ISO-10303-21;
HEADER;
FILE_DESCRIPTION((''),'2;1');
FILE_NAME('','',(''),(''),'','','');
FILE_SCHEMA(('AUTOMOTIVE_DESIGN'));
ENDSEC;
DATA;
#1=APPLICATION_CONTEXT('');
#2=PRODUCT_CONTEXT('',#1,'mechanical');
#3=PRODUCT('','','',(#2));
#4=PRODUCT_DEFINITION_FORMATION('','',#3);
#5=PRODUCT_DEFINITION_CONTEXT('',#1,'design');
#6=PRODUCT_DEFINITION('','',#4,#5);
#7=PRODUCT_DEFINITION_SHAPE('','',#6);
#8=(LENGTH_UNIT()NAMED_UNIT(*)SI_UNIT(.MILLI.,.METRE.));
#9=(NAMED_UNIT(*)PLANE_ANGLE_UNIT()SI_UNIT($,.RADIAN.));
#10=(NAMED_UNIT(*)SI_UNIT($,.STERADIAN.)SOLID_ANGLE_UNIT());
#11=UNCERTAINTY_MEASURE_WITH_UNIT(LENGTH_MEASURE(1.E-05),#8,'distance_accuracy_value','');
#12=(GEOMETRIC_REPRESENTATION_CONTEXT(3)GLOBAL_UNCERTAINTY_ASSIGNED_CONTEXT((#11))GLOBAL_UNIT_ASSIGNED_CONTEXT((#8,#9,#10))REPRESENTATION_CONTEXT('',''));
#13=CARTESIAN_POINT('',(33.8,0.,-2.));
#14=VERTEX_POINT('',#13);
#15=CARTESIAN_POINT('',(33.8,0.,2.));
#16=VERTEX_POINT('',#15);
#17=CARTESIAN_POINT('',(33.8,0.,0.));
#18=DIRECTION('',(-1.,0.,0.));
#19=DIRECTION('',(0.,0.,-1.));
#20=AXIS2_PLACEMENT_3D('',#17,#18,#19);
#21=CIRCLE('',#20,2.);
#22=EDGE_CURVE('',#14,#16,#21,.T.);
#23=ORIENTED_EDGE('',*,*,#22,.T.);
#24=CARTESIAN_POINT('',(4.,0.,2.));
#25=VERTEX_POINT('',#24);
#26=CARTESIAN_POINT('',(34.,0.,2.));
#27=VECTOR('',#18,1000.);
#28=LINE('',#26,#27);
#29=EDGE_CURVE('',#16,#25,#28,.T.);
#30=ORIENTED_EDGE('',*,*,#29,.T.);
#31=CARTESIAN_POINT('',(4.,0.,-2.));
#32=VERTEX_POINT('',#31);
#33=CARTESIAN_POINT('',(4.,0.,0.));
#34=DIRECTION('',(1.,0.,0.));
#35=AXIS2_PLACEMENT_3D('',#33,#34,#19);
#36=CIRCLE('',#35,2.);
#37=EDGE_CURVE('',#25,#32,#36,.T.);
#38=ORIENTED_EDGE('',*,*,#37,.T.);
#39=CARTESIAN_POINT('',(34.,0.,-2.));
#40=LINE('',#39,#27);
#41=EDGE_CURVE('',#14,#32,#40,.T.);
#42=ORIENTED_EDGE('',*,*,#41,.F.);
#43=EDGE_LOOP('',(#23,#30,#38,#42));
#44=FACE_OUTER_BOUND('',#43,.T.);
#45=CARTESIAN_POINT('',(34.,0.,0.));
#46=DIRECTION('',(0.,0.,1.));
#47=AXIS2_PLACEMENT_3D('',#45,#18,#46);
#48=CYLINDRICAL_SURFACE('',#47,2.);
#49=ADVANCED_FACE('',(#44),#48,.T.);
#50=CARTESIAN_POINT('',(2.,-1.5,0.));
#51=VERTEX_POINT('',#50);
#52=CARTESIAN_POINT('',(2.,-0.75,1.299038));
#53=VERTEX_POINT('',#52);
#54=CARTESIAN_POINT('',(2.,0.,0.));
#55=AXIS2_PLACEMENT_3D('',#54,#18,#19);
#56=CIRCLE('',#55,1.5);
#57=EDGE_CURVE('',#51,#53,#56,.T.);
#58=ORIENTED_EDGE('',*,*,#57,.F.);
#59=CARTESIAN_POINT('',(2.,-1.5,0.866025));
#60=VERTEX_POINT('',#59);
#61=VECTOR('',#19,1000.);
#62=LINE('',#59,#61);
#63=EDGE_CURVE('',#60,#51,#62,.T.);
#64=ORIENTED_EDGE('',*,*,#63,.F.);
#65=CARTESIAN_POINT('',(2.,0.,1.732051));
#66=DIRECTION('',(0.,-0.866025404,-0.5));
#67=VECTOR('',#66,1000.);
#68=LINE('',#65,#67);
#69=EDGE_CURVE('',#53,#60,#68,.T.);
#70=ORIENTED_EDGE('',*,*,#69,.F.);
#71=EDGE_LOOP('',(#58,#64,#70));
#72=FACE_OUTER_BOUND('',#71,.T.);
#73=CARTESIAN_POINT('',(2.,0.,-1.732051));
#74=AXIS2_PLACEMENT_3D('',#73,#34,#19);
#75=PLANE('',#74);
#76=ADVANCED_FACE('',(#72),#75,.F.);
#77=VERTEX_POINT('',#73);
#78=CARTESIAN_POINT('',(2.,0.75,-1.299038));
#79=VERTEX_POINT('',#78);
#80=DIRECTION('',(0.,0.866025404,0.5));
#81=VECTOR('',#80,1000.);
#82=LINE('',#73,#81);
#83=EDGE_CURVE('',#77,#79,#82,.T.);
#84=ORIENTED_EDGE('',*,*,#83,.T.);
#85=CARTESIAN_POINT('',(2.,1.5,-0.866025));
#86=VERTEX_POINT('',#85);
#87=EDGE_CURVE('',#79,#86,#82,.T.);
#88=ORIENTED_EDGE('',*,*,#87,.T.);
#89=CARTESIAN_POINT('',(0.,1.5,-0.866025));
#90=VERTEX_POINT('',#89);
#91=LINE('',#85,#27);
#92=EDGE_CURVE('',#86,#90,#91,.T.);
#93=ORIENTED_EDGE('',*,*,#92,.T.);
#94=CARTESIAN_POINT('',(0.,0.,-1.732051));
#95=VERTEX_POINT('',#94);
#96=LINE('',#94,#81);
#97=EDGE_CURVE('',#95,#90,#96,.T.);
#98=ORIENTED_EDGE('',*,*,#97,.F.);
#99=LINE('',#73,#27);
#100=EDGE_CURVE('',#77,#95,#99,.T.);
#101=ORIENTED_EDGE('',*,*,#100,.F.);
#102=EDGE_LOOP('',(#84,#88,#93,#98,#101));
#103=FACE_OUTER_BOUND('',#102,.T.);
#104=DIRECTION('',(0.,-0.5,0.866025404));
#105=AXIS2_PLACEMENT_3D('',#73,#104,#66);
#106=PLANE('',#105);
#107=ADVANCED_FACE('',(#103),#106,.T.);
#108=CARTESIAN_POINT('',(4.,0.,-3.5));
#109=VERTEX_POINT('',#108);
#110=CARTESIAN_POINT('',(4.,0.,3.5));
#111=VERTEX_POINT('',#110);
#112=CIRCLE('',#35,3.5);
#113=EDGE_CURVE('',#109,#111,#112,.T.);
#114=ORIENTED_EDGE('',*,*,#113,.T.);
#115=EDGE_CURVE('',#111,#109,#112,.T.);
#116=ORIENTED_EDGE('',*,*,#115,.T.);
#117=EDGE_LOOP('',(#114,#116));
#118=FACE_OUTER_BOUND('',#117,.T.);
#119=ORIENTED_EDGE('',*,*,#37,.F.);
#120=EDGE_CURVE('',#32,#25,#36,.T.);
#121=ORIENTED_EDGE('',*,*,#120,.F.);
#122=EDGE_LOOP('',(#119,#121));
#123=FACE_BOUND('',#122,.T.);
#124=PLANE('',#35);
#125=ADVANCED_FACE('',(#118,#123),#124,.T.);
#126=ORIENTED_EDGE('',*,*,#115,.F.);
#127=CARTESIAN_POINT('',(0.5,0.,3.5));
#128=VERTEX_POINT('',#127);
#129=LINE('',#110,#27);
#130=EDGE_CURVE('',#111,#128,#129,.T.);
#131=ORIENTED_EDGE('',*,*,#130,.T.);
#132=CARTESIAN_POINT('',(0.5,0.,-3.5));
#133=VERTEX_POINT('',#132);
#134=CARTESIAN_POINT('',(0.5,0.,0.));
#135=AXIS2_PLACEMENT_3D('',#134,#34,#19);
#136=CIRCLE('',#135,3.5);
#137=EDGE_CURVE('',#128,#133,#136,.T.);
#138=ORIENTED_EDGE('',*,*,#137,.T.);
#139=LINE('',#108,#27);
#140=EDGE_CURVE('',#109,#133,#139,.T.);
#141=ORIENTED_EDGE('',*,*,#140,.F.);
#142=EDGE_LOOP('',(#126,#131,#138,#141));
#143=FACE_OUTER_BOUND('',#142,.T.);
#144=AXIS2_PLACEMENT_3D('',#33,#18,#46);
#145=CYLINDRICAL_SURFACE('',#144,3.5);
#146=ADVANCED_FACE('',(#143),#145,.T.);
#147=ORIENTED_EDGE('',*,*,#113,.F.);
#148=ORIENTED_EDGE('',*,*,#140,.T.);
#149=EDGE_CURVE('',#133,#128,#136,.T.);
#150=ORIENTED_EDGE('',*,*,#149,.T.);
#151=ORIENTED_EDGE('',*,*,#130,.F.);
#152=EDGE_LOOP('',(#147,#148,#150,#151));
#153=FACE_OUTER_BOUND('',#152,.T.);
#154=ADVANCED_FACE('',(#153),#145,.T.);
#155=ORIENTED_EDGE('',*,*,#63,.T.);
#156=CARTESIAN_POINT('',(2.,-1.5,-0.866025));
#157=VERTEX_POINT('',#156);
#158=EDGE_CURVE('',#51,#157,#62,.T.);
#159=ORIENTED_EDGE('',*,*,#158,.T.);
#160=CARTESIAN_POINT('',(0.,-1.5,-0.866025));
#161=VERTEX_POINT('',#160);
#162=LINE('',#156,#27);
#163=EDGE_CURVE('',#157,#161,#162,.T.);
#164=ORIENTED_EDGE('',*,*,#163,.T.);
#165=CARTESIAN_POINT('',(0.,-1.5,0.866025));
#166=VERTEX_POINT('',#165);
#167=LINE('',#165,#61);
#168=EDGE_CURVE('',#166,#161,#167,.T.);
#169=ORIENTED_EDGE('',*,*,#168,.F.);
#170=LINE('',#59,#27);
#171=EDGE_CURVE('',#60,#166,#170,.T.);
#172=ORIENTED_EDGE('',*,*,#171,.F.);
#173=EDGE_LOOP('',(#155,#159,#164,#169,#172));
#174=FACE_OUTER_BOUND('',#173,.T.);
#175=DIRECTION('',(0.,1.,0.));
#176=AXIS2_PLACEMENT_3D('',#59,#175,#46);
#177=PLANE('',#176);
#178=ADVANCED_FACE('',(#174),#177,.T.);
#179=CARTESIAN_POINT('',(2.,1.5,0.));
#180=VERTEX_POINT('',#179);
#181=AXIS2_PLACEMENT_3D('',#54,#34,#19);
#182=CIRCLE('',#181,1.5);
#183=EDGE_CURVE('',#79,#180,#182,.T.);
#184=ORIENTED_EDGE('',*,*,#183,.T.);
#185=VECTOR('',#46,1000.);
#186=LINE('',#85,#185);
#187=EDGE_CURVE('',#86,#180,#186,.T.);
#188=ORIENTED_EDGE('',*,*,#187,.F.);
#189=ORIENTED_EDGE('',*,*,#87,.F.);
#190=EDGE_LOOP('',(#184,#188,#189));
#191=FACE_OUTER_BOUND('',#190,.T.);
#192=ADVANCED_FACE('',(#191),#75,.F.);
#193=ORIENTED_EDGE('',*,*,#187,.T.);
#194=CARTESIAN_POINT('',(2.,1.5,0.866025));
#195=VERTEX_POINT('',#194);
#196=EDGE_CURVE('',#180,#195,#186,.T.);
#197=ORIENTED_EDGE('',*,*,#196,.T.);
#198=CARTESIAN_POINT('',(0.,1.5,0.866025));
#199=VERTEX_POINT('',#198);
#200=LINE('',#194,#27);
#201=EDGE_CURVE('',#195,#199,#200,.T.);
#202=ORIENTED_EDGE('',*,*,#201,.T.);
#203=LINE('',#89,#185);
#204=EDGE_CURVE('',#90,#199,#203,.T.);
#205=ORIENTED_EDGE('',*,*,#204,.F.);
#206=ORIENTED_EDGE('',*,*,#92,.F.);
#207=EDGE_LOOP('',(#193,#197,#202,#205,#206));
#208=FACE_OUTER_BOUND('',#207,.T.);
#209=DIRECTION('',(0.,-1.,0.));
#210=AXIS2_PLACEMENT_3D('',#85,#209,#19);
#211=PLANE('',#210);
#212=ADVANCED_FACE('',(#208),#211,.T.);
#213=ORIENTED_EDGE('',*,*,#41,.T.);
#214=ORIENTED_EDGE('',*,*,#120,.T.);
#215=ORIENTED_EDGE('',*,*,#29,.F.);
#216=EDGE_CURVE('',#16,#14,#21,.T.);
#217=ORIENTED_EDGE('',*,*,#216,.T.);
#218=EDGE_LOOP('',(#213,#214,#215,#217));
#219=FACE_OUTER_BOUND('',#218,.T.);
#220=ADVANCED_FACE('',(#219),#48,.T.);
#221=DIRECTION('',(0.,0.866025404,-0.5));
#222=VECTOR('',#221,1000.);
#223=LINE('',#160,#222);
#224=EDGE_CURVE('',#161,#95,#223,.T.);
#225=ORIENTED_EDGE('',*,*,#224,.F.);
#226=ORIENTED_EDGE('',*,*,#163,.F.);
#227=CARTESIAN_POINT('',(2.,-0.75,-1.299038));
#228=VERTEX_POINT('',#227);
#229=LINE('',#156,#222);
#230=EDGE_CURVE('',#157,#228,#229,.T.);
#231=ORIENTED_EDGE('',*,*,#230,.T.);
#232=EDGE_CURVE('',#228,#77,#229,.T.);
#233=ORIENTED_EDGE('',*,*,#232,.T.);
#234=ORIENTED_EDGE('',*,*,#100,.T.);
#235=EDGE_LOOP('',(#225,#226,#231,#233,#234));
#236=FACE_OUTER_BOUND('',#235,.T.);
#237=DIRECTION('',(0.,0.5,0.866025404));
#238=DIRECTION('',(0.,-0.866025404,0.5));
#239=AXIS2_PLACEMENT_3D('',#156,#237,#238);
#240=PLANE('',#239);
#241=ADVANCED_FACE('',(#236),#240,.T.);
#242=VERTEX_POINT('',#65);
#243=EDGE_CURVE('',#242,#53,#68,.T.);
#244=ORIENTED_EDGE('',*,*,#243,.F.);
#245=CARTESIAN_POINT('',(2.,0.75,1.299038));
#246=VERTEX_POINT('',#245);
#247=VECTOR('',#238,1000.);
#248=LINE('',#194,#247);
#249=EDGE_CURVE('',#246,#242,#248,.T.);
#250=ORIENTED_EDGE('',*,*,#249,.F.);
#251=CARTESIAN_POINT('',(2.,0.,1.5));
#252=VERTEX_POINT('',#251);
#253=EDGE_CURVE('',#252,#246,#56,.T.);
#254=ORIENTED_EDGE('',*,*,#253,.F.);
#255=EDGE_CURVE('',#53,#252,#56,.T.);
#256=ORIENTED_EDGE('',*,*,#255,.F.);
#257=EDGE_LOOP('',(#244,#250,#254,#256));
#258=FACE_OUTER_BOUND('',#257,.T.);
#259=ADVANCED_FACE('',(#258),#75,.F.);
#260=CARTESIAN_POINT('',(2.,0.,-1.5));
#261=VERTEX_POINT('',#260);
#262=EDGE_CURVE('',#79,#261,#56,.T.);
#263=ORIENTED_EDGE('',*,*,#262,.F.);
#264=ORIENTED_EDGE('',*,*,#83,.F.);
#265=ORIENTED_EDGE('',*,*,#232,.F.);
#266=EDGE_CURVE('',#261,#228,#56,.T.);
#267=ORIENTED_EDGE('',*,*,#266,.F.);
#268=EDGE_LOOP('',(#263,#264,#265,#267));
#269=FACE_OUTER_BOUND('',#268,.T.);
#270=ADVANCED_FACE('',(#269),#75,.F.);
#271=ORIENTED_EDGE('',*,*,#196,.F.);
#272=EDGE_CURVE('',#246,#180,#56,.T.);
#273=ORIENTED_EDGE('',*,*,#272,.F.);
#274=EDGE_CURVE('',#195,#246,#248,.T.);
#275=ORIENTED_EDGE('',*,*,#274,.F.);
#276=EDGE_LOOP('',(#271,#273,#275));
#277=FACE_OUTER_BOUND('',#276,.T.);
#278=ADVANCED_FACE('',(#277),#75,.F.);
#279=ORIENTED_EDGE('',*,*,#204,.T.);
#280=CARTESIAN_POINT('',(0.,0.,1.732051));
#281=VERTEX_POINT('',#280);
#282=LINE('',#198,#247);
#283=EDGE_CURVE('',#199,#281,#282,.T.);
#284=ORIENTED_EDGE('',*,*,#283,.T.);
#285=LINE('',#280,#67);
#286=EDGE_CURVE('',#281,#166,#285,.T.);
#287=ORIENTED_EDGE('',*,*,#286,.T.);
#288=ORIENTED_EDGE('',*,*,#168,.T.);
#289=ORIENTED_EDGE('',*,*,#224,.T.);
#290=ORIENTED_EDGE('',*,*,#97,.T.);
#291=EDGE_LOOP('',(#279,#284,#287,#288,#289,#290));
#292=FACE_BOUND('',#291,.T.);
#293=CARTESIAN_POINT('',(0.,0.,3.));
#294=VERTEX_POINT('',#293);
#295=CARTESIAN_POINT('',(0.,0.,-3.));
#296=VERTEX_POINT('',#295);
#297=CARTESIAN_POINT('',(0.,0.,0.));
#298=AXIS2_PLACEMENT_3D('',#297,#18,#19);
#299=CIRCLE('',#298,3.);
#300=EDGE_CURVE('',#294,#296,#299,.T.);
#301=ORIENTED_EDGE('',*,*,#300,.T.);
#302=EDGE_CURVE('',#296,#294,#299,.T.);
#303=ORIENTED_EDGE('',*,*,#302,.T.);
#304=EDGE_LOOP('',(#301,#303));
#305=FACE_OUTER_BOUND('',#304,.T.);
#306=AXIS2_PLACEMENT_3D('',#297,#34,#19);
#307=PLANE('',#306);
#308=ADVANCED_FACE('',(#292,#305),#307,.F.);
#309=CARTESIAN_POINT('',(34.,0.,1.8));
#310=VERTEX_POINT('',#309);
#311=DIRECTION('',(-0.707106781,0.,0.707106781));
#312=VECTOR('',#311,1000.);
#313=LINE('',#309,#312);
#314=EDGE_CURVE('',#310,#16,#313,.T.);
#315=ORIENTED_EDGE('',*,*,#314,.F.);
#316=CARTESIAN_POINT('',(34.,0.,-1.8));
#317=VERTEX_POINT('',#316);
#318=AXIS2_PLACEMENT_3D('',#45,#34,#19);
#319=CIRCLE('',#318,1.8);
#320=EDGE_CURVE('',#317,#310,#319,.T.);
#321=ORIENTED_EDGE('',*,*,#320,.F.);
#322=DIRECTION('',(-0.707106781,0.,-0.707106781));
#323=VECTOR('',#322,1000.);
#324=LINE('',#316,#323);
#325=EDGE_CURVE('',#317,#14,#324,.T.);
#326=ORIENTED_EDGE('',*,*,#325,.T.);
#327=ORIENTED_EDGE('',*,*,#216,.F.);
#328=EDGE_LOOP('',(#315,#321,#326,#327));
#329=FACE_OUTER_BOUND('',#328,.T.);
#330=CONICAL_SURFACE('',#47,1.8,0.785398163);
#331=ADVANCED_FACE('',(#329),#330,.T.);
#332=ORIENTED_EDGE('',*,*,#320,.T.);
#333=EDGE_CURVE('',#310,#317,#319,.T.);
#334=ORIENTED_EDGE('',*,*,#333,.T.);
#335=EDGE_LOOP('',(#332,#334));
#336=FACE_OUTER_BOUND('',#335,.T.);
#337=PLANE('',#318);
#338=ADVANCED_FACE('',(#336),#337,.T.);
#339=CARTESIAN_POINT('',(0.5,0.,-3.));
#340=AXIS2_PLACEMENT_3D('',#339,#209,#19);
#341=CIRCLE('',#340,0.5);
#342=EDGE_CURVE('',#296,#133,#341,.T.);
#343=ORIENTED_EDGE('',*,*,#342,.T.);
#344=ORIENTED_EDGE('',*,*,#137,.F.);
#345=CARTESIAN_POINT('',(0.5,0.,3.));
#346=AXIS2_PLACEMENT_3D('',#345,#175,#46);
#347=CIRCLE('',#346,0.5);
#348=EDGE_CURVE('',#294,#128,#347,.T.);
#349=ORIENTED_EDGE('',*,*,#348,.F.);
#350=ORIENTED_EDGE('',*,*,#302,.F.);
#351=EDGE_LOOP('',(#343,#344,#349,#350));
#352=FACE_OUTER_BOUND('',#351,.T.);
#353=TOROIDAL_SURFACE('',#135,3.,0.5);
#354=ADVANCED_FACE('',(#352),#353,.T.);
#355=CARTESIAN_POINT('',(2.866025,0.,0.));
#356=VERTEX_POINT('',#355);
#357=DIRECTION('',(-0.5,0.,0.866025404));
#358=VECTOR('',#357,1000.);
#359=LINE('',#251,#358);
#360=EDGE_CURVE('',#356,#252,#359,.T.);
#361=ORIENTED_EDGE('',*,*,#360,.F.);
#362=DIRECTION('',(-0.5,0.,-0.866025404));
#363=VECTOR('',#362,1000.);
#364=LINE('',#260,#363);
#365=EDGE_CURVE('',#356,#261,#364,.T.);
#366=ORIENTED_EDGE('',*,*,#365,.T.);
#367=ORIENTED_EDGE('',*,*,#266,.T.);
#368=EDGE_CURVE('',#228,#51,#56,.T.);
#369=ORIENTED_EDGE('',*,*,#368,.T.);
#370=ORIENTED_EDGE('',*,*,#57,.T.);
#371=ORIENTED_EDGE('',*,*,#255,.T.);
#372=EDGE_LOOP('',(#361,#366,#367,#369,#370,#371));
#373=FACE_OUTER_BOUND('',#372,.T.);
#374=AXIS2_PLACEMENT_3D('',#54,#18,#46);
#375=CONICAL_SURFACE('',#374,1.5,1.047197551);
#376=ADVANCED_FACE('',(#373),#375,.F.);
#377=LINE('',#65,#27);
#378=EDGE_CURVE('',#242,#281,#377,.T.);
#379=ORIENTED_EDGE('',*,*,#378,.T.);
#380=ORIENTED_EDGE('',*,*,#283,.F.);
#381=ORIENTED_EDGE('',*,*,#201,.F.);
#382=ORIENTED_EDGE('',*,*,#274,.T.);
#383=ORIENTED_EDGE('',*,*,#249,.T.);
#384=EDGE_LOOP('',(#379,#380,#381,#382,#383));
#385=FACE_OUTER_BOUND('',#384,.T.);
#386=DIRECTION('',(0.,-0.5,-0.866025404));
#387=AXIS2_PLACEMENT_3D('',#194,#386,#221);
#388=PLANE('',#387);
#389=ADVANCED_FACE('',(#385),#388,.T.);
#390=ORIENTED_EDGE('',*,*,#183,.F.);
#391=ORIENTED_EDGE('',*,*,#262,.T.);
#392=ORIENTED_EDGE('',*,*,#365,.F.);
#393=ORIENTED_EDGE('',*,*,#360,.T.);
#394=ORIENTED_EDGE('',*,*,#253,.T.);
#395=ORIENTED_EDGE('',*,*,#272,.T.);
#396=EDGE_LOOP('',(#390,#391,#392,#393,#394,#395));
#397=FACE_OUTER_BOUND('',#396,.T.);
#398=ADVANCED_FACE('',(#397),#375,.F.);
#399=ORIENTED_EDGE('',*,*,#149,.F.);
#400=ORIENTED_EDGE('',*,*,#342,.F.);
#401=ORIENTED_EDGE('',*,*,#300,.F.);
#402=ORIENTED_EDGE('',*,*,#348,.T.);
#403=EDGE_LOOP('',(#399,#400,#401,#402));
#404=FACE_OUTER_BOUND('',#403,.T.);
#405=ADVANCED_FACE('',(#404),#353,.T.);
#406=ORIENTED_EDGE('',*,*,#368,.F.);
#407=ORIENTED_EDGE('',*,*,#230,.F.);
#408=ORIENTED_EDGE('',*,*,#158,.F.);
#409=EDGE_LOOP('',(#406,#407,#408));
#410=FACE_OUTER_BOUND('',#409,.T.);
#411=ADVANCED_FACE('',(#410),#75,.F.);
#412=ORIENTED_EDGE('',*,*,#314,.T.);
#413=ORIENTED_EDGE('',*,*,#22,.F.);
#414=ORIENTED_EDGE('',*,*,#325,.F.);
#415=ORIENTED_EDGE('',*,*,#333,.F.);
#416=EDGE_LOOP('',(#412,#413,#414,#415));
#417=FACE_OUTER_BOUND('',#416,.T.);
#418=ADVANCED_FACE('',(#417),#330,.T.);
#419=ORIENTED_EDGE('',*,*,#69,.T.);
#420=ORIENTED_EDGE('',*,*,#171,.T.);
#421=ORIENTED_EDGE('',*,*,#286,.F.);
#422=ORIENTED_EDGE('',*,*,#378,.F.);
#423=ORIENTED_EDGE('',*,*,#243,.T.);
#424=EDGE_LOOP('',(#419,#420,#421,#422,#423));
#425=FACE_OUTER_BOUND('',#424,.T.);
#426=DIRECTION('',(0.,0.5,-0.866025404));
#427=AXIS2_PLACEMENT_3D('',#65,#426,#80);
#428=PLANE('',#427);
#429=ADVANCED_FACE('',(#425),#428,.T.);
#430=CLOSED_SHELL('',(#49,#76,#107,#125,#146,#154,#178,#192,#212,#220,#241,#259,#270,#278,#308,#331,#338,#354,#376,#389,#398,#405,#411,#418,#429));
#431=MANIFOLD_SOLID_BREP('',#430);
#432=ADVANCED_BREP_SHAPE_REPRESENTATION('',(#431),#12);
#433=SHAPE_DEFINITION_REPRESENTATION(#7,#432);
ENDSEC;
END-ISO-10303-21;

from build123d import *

# Parameters (mm, degrees)
SKETCH1_R           = 3.5
BASEHEAD_DEPTH      = 4
SKETCH2_R           = 2
BASEBODY_DEPTH      = 30
HEXAGONSOCKET_DEPTH = 2
TOPFILLET_R         = 0.5
CHAMFER1_SIZE       = 0.2


with BuildPart() as part:
    # Sketch1 → BaseHead (new body)
    with BuildSketch(Plane(origin=(0, 0, 0), x_dir=(0, 0, -1), z_dir=(1, 0, 0))):
        Circle(SKETCH1_R)
    extrude(amount=BASEHEAD_DEPTH)

    # Sketch2 → BaseBody (add)
    with BuildSketch(Plane(origin=(4, 0, 0), x_dir=(0, 0, -1), z_dir=(1, 0, 0))):
        Circle(SKETCH2_R)
    extrude(amount=BASEBODY_DEPTH)

    # Sketch3 → HexagonSocket (cut)
    with BuildSketch(Plane(origin=(0, 0, 0), x_dir=(0, 0, -1), z_dir=(1, 0, 0))):
        Polygon((1.732050808, 0), (0.866025404, 1.5), (-0.866025404, 1.5), (-1.732050808, 0), (-0.866025404, -1.5), (0.866025404, -1.5), align=None)
    extrude(amount=HEXAGONSOCKET_DEPTH, mode=Mode.SUBTRACT)

    # Sketch4 → Cut-Revolve1 (revolve, cut)
    with BuildSketch(Plane(origin=(-4.19613823, 0.75, 0), x_dir=(-1, 0, 0), z_dir=(0, 0, 1)), mode=Mode.PRIVATE) as cut_revolve1_sk:
        Polygon((-6.19613823, 2.25), (-7.062163633, 0.75), (-6.19613823, 0.75), align=None)
    revolve(cut_revolve1_sk.sketch.rotate(Axis((0.838992387, 0, 0), (-1, 0, 0)), 90), axis=Axis((0.838992387, 0, 0), (-1, 0, 0)), mode=Mode.SUBTRACT)

    # TopFillet
    topfillet_edges = [part.edges().sort_by_distance(p)[0] for p in [
        (0, 0, 3.5),
    ]]
    fillet(topfillet_edges, radius=TOPFILLET_R)

    # Chamfer1
    chamfer1_edges = [part.edges().sort_by_distance(p)[0] for p in [
        (34, 0, 2),
    ]]
    chamfer(chamfer1_edges, length=CHAMFER1_SIZE)


solid = part.part
